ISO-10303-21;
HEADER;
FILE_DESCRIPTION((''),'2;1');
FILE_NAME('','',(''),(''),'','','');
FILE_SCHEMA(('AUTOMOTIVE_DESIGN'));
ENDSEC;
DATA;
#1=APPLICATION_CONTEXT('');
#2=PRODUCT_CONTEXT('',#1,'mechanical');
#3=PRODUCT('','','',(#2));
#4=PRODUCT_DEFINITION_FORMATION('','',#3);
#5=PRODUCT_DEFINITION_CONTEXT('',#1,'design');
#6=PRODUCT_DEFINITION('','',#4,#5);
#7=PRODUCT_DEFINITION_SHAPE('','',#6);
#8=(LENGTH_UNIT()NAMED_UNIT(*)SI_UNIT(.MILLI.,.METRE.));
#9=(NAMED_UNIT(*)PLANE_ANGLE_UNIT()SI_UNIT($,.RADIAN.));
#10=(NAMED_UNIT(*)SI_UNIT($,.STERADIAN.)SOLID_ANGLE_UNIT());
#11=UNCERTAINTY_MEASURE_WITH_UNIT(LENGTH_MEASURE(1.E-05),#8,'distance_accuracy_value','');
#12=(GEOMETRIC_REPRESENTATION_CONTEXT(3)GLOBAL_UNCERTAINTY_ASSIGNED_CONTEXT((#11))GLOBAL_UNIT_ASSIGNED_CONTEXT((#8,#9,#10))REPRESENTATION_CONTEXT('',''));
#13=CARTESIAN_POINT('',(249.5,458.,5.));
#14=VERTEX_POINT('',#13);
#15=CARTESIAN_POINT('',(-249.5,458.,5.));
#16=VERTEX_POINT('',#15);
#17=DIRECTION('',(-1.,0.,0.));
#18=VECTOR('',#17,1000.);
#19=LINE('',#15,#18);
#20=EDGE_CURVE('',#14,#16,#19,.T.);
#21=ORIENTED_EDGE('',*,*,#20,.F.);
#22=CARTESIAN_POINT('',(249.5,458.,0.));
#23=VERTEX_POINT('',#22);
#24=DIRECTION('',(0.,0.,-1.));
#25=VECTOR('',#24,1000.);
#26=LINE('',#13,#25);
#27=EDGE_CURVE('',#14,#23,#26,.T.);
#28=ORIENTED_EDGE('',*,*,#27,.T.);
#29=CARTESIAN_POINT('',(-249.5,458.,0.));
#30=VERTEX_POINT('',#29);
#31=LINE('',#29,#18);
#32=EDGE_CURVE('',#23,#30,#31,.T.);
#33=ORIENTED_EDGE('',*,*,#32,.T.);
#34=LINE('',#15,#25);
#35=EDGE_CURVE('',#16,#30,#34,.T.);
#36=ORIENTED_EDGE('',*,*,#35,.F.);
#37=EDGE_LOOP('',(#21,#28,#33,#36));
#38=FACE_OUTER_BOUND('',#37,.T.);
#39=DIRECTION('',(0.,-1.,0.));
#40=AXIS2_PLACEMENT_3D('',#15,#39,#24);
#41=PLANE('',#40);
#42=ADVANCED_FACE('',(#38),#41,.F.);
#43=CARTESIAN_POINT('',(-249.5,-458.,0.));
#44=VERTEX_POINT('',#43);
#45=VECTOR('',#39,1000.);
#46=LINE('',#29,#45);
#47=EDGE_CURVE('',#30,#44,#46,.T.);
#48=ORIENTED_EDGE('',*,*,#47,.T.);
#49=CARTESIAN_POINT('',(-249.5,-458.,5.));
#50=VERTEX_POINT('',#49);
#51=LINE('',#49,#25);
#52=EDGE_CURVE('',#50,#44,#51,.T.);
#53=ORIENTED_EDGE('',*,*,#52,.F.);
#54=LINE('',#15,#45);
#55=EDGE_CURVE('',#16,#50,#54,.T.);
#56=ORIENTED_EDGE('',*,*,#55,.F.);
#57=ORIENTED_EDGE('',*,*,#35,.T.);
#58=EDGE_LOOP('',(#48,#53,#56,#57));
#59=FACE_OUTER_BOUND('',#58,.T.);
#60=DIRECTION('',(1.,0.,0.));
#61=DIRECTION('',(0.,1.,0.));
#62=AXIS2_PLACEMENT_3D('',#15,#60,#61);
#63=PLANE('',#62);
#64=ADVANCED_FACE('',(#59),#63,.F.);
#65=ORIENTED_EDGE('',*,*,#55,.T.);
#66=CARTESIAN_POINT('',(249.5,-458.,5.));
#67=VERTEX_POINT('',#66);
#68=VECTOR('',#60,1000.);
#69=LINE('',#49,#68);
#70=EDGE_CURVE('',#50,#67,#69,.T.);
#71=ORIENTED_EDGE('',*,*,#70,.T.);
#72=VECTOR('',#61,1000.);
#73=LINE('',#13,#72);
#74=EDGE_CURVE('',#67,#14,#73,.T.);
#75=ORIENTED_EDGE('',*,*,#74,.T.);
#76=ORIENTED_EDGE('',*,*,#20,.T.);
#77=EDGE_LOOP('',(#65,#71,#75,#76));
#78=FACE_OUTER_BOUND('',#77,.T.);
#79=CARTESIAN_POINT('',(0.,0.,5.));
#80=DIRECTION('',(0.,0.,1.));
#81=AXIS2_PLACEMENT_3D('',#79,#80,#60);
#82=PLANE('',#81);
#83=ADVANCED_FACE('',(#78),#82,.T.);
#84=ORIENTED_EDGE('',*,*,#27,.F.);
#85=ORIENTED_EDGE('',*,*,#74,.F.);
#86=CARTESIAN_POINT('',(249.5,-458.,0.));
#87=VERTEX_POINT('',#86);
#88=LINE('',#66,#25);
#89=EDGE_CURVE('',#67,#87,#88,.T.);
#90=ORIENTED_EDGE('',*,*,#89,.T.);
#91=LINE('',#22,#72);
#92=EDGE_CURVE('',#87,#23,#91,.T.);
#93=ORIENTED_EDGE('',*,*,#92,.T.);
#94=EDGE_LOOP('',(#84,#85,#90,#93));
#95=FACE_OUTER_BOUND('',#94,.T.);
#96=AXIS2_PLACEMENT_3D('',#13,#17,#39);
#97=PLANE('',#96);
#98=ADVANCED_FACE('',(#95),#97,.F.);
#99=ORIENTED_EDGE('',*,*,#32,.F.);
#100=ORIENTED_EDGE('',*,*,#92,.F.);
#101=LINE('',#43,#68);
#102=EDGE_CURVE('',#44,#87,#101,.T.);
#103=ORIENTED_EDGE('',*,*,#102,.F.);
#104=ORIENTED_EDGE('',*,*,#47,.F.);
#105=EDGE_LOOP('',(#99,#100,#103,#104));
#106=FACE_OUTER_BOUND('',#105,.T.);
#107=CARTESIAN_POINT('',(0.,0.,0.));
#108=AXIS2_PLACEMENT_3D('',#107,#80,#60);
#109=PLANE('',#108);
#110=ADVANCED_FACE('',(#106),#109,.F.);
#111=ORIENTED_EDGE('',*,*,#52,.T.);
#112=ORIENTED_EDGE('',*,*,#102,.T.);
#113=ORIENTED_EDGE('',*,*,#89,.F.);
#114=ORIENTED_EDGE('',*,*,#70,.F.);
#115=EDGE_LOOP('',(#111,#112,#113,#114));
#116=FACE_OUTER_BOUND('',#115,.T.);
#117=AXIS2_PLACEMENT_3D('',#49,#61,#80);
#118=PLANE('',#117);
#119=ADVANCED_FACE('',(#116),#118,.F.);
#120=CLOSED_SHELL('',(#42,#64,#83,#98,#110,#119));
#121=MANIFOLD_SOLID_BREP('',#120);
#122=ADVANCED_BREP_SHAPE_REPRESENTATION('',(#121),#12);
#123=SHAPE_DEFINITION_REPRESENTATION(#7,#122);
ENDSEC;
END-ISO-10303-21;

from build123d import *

# Parameters (mm, degrees)
SKETCH_1_W      = 499
SKETCH_1_H      = 916
EXTRUDE_1_DEPTH = 5


with BuildPart() as part:
    # 草图1 → 凸台-拉伸1 (new body)
    with BuildSketch(Plane.XY):
        Rectangle(SKETCH_1_W, SKETCH_1_H)
    extrude(amount=EXTRUDE_1_DEPTH)


solid = part.part
